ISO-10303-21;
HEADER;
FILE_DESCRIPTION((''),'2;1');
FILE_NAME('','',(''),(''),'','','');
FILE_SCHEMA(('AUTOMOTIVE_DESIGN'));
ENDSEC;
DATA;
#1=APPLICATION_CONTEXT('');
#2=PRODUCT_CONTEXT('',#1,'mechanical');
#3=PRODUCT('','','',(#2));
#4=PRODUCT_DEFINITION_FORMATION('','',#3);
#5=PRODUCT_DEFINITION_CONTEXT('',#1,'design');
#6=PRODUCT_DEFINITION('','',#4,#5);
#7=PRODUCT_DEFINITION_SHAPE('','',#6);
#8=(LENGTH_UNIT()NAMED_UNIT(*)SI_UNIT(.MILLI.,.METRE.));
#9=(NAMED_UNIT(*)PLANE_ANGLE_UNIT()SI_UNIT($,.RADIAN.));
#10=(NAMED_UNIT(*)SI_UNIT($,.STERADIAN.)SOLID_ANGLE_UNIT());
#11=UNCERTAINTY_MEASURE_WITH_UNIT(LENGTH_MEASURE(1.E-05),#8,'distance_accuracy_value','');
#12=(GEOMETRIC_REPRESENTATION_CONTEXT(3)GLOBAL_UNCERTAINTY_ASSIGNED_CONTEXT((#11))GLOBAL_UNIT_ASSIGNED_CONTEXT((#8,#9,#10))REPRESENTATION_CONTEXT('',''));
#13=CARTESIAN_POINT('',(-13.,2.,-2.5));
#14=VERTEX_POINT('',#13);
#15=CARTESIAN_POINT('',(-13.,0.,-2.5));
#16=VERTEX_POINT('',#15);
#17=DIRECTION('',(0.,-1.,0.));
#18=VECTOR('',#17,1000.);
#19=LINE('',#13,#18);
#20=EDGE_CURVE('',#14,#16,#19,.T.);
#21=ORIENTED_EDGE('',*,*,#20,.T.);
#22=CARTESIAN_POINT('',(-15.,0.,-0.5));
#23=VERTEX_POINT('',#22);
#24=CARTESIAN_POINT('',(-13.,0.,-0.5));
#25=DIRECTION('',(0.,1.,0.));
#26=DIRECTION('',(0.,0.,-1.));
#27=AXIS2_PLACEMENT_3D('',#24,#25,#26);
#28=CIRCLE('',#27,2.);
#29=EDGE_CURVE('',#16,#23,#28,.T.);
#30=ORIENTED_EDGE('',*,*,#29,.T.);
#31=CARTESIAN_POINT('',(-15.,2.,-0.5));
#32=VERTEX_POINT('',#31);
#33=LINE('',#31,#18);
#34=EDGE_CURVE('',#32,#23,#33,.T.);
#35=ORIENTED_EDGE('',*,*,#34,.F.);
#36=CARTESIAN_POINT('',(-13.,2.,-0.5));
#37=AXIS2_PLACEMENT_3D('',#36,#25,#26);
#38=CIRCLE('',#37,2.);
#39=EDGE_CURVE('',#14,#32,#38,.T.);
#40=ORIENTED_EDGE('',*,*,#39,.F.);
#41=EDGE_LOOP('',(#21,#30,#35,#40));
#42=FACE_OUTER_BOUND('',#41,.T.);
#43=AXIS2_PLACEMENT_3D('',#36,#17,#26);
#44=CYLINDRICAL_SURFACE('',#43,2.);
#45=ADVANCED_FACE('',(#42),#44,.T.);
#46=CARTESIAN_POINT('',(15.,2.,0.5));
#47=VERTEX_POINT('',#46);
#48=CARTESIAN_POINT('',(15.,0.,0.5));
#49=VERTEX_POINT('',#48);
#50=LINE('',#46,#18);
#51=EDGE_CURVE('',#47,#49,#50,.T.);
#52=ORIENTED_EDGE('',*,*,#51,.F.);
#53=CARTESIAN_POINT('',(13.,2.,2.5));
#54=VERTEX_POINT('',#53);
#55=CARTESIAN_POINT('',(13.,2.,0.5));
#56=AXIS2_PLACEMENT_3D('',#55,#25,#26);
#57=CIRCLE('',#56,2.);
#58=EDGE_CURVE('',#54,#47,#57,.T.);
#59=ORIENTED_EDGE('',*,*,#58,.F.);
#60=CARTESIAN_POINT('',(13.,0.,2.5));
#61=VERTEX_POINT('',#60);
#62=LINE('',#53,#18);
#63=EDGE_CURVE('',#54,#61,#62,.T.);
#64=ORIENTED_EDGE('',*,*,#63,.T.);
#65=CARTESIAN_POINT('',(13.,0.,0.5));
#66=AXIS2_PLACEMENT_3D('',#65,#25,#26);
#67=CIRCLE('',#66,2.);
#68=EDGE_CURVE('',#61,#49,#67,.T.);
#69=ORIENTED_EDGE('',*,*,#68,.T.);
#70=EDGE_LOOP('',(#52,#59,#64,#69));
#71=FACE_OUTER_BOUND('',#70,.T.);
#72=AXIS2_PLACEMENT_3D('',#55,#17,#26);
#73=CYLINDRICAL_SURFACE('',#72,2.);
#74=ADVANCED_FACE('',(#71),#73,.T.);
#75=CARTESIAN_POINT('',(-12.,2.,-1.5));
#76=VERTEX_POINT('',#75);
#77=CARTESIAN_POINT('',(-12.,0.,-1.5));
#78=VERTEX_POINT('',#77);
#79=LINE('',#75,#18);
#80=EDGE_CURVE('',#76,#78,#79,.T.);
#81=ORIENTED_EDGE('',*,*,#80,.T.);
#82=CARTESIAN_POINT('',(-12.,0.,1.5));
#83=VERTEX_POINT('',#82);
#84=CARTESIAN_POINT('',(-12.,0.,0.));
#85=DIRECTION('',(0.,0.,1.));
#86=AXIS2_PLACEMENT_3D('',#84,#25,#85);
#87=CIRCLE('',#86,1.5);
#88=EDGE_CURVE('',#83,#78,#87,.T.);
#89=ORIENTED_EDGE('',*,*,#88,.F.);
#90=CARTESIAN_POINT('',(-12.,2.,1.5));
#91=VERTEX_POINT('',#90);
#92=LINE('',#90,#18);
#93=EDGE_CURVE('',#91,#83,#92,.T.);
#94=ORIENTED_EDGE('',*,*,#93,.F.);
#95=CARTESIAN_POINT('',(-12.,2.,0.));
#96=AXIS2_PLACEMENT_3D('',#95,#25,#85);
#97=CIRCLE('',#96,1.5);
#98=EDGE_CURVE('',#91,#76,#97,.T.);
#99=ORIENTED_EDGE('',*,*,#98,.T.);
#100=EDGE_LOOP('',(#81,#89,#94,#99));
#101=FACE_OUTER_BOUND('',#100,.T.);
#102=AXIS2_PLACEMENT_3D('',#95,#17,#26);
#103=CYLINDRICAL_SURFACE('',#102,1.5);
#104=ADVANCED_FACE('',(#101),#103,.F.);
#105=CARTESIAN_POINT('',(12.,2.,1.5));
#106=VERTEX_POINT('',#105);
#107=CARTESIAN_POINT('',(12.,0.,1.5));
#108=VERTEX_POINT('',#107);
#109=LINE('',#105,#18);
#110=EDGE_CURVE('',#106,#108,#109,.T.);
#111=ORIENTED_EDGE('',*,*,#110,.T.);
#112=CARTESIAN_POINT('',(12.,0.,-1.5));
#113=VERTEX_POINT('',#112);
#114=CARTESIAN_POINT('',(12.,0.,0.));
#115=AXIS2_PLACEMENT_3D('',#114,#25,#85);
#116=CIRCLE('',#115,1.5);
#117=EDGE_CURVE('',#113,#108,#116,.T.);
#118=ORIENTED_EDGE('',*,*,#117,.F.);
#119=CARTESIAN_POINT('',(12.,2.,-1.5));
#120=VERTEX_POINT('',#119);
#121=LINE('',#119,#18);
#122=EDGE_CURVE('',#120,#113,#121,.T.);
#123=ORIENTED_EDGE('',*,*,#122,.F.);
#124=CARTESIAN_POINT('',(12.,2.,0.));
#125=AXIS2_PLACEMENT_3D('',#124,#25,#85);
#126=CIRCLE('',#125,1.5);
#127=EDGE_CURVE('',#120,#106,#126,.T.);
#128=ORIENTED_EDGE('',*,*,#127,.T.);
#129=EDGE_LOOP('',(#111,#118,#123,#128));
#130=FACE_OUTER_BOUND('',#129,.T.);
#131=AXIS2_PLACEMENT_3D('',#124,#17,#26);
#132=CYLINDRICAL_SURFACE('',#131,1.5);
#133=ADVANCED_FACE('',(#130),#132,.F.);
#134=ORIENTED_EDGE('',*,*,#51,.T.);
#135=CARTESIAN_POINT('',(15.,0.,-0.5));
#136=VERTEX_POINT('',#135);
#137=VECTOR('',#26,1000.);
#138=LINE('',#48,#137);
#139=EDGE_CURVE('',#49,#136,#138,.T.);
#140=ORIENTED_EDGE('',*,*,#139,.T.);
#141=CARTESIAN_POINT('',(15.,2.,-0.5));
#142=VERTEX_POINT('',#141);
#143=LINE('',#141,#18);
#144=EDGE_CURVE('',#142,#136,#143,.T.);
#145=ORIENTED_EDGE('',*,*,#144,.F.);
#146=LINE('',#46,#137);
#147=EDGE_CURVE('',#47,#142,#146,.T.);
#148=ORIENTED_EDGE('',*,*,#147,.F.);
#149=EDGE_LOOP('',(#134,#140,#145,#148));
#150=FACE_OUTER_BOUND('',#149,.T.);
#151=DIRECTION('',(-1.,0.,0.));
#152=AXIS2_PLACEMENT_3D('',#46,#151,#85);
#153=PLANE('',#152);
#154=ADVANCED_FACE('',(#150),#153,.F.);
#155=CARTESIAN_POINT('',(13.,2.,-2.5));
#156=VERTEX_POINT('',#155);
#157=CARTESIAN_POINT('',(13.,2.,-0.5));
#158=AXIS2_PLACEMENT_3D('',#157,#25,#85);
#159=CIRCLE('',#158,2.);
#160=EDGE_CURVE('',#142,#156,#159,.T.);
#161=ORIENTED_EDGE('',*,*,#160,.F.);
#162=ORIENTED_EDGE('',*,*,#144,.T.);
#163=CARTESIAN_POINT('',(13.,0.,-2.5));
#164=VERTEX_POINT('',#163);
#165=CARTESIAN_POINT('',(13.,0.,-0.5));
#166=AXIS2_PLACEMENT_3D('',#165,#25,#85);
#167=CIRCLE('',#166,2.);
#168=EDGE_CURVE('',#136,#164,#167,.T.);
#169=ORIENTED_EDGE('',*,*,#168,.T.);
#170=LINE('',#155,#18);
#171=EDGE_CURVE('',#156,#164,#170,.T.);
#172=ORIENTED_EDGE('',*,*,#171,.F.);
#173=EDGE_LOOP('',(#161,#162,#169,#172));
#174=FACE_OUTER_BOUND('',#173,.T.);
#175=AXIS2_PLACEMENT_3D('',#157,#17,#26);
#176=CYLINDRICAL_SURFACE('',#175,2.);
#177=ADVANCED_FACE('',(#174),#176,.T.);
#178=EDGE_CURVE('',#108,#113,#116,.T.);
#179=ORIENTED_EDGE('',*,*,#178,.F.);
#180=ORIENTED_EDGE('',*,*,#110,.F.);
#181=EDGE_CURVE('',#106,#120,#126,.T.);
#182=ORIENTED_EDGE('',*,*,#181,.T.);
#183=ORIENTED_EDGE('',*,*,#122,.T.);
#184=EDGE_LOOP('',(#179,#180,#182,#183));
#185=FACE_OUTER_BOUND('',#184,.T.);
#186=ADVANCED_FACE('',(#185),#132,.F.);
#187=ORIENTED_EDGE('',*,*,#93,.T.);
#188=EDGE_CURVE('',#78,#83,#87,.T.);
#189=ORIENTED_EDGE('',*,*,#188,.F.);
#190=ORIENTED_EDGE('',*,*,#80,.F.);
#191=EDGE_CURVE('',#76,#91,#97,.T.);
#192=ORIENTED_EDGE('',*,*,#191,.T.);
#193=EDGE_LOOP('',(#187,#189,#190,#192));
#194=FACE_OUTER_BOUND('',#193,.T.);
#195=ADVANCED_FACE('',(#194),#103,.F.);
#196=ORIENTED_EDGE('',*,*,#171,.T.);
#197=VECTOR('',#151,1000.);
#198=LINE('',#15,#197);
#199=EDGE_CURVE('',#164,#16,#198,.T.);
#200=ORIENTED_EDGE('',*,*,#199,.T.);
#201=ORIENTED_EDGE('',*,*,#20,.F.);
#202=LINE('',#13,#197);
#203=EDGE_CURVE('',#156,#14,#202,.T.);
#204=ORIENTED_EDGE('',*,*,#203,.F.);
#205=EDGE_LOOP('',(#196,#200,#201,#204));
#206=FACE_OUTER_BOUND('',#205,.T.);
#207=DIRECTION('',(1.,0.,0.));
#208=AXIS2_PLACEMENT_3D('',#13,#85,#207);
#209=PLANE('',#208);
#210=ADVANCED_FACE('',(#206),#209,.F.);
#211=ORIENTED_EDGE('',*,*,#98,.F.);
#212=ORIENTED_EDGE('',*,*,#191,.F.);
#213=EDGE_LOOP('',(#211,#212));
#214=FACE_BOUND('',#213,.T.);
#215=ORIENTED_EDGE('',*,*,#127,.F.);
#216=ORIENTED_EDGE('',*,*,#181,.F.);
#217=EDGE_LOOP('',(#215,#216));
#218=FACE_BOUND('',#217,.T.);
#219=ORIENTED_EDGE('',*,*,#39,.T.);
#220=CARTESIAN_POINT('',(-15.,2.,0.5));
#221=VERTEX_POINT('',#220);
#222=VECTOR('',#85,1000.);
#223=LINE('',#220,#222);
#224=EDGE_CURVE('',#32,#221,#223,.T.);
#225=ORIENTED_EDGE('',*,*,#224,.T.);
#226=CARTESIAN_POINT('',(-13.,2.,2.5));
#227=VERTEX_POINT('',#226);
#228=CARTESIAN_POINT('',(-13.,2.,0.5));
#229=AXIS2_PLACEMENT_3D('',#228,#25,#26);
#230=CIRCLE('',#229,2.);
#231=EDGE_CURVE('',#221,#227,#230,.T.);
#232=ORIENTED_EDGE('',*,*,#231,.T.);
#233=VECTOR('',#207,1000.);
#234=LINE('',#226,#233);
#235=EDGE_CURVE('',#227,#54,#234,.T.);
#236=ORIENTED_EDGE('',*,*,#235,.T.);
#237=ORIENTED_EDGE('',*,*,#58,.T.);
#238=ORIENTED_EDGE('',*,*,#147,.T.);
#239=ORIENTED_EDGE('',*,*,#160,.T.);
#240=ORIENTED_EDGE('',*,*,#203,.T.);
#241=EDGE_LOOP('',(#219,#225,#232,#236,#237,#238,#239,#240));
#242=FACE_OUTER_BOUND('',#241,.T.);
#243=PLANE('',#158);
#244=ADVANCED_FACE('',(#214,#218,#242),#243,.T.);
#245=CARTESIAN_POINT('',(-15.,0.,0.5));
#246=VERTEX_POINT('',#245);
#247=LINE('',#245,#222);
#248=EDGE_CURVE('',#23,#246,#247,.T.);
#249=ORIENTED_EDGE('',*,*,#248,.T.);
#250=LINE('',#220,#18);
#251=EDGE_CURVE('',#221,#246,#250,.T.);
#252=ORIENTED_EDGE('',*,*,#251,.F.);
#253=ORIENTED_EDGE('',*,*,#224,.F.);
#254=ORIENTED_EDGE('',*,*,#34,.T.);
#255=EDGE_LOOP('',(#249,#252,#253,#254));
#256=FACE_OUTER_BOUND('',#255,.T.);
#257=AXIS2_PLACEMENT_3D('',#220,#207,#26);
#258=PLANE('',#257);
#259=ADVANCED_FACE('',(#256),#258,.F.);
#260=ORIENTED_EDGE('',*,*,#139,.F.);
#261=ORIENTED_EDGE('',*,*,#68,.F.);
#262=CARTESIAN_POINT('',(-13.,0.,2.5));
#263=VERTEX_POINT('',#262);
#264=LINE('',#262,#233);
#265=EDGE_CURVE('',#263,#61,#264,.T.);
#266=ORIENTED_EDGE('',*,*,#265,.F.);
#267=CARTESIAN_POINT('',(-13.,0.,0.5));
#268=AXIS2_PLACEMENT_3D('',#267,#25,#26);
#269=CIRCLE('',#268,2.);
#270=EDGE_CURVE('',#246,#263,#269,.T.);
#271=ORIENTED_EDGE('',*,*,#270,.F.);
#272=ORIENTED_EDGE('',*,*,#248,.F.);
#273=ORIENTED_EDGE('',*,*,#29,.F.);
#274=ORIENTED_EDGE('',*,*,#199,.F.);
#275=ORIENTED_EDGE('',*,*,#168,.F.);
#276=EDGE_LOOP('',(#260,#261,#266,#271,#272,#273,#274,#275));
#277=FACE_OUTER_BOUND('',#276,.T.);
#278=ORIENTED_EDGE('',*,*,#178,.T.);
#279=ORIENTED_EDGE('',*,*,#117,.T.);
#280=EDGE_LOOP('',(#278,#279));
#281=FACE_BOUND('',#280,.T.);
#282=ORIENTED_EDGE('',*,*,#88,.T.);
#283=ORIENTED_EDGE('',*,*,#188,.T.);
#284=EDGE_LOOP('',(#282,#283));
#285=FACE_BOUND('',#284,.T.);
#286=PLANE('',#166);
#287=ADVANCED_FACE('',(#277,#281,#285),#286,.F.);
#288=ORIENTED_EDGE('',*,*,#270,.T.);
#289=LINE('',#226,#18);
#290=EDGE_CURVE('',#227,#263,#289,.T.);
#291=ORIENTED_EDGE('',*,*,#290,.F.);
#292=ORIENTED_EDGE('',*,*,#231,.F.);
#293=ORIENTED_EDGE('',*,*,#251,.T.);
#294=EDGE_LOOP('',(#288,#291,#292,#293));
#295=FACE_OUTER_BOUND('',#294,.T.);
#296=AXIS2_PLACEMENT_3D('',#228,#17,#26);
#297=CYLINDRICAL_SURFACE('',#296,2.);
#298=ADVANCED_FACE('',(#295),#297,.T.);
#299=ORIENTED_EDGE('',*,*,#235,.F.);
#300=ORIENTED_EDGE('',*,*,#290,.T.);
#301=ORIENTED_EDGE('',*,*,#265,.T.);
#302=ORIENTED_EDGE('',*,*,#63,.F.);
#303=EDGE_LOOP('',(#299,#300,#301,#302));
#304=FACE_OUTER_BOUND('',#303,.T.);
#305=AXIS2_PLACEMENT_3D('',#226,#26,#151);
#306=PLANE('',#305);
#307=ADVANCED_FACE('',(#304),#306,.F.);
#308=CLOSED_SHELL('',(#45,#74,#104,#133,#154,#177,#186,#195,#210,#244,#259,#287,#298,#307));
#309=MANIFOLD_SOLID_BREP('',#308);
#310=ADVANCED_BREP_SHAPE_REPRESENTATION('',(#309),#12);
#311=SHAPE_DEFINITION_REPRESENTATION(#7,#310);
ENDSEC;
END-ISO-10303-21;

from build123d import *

# Parameters (mm, degrees)
SKETCH1_R           = 1.5
BOSS_EXTRUDE1_DEPTH = 2


with BuildPart() as part:
    # Sketch1 → Boss-Extrude1 (new body)
    with BuildSketch(Plane(origin=(0, 0, 0), x_dir=(1, 0, 0), z_dir=(0, 1, 0))):
        with BuildLine():
            Line((-13, -2.5), (13, -2.5))
            ThreePointArc((13, -2.5), (14.414213562, -1.914213562), (15, -0.5))
            Line((15, -0.5), (15, 0.5))
            ThreePointArc((15, 0.5), (14.414213562, 1.914213562), (13, 2.5))
            Line((13, 2.5), (-13, 2.5))
            ThreePointArc((-13, 2.5), (-14.414213562, 1.914213562), (-15, 0.5))
            Line((-15, 0.5), (-15, -0.5))
            ThreePointArc((-15, -0.5), (-14.414213562, -1.914213562), (-13, -2.5))
        make_face()
        with Locations(Location((12, 0, 0), (0, 0, 270))):
            Circle(SKETCH1_R, mode=Mode.SUBTRACT)
        with Locations(Location((-12, 0, 0), (0, 0, 270))):
            Circle(SKETCH1_R, mode=Mode.SUBTRACT)
    extrude(amount=BOSS_EXTRUDE1_DEPTH)


solid = part.part
